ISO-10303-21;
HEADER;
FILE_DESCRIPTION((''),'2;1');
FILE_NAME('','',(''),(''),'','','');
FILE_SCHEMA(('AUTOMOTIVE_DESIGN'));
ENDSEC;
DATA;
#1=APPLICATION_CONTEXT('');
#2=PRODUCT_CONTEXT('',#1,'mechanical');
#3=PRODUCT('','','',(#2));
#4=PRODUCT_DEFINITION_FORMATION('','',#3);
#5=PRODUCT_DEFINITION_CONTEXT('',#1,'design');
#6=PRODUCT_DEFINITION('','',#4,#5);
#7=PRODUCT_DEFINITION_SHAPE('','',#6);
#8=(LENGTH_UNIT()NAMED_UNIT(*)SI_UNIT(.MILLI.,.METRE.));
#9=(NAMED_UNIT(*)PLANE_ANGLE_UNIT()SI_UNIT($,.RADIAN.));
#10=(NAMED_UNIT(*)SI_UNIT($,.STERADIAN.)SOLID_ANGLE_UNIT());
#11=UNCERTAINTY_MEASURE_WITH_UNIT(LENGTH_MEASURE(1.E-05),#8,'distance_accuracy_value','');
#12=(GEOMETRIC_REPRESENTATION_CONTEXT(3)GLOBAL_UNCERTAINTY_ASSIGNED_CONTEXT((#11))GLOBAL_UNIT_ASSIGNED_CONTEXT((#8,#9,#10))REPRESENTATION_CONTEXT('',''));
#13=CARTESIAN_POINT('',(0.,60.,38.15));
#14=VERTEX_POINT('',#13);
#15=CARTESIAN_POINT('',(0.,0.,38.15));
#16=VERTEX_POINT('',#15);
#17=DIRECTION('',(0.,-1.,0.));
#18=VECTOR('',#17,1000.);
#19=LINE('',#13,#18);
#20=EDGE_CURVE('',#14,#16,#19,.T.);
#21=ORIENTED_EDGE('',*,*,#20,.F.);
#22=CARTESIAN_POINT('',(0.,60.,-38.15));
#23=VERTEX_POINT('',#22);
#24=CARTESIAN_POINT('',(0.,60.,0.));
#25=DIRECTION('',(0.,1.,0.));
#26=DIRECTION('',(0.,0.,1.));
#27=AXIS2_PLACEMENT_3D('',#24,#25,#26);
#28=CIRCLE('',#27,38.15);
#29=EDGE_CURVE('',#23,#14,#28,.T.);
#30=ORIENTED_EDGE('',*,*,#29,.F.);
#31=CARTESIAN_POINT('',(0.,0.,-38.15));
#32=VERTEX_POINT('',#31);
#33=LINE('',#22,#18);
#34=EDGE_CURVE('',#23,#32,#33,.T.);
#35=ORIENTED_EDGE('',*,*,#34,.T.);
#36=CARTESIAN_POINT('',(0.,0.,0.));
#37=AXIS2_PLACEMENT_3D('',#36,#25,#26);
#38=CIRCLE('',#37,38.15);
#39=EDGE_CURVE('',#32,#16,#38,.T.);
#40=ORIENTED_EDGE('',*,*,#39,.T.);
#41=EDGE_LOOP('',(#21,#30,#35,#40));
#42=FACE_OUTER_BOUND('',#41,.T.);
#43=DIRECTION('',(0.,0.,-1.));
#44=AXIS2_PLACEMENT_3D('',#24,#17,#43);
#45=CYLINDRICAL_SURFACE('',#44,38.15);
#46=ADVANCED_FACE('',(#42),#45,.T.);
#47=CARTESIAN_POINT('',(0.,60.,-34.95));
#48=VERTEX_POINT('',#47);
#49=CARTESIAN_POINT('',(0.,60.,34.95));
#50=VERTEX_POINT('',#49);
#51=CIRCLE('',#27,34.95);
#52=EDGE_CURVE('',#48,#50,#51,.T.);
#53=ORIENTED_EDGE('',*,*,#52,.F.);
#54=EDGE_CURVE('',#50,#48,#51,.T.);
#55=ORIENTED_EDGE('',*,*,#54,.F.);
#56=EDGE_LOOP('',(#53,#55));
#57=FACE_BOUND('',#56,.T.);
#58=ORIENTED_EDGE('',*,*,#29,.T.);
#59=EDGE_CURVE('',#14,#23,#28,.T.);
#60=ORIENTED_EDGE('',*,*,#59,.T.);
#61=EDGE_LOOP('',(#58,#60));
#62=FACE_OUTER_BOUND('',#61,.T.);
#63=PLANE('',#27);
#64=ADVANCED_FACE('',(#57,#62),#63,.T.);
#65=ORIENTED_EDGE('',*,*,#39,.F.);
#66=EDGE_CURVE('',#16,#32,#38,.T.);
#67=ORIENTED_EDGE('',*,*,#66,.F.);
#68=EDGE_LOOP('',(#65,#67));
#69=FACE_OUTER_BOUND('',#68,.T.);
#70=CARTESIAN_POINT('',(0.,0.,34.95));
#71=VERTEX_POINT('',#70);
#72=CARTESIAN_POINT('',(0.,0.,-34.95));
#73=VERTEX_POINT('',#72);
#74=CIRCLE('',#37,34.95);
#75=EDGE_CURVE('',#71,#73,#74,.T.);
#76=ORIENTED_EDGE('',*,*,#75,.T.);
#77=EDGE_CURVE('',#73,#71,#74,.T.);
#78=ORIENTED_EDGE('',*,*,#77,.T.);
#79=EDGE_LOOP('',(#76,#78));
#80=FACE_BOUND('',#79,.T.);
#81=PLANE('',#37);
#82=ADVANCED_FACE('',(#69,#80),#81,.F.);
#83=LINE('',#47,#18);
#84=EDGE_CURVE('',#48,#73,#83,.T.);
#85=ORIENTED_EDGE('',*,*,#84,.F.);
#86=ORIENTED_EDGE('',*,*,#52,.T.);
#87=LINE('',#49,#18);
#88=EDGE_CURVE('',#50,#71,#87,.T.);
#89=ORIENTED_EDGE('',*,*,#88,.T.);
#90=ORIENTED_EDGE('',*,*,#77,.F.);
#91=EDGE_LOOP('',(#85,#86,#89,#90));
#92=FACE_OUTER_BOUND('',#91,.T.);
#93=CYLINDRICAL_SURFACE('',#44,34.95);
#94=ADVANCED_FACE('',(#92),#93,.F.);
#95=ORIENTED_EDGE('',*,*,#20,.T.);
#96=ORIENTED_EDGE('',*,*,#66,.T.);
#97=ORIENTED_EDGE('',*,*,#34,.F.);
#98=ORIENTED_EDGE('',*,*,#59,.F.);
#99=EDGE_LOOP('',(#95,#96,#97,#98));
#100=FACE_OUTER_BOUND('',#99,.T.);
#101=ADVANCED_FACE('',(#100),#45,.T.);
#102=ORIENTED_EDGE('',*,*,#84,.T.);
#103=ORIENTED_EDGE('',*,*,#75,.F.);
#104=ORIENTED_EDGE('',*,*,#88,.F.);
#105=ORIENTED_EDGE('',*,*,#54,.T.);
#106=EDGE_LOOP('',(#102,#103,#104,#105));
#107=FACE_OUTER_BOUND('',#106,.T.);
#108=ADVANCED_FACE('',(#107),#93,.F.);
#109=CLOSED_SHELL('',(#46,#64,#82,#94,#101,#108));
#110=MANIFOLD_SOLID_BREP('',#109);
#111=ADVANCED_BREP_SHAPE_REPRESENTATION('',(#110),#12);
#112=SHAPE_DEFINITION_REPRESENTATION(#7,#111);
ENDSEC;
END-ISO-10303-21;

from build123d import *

# Parameters (mm, degrees)
SKETCH1_R           = 38.15
SKETCH1_R_2         = 34.95
BOSS_EXTRUDE1_DEPTH = 60


with BuildPart() as part:
    # Sketch1 → Boss-Extrude1 (new body)
    with BuildSketch(Plane(origin=(0, 0, 0), x_dir=(1, 0, 0), z_dir=(0, 1, 0))):
        with Locations(Location((0, 0, 0), (0, 0, 270))):
            Circle(SKETCH1_R)
        with Locations(Location((0, 0, 0), (0, 0, 270))):
            Circle(SKETCH1_R_2, mode=Mode.SUBTRACT)
    extrude(amount=BOSS_EXTRUDE1_DEPTH)


solid = part.part
